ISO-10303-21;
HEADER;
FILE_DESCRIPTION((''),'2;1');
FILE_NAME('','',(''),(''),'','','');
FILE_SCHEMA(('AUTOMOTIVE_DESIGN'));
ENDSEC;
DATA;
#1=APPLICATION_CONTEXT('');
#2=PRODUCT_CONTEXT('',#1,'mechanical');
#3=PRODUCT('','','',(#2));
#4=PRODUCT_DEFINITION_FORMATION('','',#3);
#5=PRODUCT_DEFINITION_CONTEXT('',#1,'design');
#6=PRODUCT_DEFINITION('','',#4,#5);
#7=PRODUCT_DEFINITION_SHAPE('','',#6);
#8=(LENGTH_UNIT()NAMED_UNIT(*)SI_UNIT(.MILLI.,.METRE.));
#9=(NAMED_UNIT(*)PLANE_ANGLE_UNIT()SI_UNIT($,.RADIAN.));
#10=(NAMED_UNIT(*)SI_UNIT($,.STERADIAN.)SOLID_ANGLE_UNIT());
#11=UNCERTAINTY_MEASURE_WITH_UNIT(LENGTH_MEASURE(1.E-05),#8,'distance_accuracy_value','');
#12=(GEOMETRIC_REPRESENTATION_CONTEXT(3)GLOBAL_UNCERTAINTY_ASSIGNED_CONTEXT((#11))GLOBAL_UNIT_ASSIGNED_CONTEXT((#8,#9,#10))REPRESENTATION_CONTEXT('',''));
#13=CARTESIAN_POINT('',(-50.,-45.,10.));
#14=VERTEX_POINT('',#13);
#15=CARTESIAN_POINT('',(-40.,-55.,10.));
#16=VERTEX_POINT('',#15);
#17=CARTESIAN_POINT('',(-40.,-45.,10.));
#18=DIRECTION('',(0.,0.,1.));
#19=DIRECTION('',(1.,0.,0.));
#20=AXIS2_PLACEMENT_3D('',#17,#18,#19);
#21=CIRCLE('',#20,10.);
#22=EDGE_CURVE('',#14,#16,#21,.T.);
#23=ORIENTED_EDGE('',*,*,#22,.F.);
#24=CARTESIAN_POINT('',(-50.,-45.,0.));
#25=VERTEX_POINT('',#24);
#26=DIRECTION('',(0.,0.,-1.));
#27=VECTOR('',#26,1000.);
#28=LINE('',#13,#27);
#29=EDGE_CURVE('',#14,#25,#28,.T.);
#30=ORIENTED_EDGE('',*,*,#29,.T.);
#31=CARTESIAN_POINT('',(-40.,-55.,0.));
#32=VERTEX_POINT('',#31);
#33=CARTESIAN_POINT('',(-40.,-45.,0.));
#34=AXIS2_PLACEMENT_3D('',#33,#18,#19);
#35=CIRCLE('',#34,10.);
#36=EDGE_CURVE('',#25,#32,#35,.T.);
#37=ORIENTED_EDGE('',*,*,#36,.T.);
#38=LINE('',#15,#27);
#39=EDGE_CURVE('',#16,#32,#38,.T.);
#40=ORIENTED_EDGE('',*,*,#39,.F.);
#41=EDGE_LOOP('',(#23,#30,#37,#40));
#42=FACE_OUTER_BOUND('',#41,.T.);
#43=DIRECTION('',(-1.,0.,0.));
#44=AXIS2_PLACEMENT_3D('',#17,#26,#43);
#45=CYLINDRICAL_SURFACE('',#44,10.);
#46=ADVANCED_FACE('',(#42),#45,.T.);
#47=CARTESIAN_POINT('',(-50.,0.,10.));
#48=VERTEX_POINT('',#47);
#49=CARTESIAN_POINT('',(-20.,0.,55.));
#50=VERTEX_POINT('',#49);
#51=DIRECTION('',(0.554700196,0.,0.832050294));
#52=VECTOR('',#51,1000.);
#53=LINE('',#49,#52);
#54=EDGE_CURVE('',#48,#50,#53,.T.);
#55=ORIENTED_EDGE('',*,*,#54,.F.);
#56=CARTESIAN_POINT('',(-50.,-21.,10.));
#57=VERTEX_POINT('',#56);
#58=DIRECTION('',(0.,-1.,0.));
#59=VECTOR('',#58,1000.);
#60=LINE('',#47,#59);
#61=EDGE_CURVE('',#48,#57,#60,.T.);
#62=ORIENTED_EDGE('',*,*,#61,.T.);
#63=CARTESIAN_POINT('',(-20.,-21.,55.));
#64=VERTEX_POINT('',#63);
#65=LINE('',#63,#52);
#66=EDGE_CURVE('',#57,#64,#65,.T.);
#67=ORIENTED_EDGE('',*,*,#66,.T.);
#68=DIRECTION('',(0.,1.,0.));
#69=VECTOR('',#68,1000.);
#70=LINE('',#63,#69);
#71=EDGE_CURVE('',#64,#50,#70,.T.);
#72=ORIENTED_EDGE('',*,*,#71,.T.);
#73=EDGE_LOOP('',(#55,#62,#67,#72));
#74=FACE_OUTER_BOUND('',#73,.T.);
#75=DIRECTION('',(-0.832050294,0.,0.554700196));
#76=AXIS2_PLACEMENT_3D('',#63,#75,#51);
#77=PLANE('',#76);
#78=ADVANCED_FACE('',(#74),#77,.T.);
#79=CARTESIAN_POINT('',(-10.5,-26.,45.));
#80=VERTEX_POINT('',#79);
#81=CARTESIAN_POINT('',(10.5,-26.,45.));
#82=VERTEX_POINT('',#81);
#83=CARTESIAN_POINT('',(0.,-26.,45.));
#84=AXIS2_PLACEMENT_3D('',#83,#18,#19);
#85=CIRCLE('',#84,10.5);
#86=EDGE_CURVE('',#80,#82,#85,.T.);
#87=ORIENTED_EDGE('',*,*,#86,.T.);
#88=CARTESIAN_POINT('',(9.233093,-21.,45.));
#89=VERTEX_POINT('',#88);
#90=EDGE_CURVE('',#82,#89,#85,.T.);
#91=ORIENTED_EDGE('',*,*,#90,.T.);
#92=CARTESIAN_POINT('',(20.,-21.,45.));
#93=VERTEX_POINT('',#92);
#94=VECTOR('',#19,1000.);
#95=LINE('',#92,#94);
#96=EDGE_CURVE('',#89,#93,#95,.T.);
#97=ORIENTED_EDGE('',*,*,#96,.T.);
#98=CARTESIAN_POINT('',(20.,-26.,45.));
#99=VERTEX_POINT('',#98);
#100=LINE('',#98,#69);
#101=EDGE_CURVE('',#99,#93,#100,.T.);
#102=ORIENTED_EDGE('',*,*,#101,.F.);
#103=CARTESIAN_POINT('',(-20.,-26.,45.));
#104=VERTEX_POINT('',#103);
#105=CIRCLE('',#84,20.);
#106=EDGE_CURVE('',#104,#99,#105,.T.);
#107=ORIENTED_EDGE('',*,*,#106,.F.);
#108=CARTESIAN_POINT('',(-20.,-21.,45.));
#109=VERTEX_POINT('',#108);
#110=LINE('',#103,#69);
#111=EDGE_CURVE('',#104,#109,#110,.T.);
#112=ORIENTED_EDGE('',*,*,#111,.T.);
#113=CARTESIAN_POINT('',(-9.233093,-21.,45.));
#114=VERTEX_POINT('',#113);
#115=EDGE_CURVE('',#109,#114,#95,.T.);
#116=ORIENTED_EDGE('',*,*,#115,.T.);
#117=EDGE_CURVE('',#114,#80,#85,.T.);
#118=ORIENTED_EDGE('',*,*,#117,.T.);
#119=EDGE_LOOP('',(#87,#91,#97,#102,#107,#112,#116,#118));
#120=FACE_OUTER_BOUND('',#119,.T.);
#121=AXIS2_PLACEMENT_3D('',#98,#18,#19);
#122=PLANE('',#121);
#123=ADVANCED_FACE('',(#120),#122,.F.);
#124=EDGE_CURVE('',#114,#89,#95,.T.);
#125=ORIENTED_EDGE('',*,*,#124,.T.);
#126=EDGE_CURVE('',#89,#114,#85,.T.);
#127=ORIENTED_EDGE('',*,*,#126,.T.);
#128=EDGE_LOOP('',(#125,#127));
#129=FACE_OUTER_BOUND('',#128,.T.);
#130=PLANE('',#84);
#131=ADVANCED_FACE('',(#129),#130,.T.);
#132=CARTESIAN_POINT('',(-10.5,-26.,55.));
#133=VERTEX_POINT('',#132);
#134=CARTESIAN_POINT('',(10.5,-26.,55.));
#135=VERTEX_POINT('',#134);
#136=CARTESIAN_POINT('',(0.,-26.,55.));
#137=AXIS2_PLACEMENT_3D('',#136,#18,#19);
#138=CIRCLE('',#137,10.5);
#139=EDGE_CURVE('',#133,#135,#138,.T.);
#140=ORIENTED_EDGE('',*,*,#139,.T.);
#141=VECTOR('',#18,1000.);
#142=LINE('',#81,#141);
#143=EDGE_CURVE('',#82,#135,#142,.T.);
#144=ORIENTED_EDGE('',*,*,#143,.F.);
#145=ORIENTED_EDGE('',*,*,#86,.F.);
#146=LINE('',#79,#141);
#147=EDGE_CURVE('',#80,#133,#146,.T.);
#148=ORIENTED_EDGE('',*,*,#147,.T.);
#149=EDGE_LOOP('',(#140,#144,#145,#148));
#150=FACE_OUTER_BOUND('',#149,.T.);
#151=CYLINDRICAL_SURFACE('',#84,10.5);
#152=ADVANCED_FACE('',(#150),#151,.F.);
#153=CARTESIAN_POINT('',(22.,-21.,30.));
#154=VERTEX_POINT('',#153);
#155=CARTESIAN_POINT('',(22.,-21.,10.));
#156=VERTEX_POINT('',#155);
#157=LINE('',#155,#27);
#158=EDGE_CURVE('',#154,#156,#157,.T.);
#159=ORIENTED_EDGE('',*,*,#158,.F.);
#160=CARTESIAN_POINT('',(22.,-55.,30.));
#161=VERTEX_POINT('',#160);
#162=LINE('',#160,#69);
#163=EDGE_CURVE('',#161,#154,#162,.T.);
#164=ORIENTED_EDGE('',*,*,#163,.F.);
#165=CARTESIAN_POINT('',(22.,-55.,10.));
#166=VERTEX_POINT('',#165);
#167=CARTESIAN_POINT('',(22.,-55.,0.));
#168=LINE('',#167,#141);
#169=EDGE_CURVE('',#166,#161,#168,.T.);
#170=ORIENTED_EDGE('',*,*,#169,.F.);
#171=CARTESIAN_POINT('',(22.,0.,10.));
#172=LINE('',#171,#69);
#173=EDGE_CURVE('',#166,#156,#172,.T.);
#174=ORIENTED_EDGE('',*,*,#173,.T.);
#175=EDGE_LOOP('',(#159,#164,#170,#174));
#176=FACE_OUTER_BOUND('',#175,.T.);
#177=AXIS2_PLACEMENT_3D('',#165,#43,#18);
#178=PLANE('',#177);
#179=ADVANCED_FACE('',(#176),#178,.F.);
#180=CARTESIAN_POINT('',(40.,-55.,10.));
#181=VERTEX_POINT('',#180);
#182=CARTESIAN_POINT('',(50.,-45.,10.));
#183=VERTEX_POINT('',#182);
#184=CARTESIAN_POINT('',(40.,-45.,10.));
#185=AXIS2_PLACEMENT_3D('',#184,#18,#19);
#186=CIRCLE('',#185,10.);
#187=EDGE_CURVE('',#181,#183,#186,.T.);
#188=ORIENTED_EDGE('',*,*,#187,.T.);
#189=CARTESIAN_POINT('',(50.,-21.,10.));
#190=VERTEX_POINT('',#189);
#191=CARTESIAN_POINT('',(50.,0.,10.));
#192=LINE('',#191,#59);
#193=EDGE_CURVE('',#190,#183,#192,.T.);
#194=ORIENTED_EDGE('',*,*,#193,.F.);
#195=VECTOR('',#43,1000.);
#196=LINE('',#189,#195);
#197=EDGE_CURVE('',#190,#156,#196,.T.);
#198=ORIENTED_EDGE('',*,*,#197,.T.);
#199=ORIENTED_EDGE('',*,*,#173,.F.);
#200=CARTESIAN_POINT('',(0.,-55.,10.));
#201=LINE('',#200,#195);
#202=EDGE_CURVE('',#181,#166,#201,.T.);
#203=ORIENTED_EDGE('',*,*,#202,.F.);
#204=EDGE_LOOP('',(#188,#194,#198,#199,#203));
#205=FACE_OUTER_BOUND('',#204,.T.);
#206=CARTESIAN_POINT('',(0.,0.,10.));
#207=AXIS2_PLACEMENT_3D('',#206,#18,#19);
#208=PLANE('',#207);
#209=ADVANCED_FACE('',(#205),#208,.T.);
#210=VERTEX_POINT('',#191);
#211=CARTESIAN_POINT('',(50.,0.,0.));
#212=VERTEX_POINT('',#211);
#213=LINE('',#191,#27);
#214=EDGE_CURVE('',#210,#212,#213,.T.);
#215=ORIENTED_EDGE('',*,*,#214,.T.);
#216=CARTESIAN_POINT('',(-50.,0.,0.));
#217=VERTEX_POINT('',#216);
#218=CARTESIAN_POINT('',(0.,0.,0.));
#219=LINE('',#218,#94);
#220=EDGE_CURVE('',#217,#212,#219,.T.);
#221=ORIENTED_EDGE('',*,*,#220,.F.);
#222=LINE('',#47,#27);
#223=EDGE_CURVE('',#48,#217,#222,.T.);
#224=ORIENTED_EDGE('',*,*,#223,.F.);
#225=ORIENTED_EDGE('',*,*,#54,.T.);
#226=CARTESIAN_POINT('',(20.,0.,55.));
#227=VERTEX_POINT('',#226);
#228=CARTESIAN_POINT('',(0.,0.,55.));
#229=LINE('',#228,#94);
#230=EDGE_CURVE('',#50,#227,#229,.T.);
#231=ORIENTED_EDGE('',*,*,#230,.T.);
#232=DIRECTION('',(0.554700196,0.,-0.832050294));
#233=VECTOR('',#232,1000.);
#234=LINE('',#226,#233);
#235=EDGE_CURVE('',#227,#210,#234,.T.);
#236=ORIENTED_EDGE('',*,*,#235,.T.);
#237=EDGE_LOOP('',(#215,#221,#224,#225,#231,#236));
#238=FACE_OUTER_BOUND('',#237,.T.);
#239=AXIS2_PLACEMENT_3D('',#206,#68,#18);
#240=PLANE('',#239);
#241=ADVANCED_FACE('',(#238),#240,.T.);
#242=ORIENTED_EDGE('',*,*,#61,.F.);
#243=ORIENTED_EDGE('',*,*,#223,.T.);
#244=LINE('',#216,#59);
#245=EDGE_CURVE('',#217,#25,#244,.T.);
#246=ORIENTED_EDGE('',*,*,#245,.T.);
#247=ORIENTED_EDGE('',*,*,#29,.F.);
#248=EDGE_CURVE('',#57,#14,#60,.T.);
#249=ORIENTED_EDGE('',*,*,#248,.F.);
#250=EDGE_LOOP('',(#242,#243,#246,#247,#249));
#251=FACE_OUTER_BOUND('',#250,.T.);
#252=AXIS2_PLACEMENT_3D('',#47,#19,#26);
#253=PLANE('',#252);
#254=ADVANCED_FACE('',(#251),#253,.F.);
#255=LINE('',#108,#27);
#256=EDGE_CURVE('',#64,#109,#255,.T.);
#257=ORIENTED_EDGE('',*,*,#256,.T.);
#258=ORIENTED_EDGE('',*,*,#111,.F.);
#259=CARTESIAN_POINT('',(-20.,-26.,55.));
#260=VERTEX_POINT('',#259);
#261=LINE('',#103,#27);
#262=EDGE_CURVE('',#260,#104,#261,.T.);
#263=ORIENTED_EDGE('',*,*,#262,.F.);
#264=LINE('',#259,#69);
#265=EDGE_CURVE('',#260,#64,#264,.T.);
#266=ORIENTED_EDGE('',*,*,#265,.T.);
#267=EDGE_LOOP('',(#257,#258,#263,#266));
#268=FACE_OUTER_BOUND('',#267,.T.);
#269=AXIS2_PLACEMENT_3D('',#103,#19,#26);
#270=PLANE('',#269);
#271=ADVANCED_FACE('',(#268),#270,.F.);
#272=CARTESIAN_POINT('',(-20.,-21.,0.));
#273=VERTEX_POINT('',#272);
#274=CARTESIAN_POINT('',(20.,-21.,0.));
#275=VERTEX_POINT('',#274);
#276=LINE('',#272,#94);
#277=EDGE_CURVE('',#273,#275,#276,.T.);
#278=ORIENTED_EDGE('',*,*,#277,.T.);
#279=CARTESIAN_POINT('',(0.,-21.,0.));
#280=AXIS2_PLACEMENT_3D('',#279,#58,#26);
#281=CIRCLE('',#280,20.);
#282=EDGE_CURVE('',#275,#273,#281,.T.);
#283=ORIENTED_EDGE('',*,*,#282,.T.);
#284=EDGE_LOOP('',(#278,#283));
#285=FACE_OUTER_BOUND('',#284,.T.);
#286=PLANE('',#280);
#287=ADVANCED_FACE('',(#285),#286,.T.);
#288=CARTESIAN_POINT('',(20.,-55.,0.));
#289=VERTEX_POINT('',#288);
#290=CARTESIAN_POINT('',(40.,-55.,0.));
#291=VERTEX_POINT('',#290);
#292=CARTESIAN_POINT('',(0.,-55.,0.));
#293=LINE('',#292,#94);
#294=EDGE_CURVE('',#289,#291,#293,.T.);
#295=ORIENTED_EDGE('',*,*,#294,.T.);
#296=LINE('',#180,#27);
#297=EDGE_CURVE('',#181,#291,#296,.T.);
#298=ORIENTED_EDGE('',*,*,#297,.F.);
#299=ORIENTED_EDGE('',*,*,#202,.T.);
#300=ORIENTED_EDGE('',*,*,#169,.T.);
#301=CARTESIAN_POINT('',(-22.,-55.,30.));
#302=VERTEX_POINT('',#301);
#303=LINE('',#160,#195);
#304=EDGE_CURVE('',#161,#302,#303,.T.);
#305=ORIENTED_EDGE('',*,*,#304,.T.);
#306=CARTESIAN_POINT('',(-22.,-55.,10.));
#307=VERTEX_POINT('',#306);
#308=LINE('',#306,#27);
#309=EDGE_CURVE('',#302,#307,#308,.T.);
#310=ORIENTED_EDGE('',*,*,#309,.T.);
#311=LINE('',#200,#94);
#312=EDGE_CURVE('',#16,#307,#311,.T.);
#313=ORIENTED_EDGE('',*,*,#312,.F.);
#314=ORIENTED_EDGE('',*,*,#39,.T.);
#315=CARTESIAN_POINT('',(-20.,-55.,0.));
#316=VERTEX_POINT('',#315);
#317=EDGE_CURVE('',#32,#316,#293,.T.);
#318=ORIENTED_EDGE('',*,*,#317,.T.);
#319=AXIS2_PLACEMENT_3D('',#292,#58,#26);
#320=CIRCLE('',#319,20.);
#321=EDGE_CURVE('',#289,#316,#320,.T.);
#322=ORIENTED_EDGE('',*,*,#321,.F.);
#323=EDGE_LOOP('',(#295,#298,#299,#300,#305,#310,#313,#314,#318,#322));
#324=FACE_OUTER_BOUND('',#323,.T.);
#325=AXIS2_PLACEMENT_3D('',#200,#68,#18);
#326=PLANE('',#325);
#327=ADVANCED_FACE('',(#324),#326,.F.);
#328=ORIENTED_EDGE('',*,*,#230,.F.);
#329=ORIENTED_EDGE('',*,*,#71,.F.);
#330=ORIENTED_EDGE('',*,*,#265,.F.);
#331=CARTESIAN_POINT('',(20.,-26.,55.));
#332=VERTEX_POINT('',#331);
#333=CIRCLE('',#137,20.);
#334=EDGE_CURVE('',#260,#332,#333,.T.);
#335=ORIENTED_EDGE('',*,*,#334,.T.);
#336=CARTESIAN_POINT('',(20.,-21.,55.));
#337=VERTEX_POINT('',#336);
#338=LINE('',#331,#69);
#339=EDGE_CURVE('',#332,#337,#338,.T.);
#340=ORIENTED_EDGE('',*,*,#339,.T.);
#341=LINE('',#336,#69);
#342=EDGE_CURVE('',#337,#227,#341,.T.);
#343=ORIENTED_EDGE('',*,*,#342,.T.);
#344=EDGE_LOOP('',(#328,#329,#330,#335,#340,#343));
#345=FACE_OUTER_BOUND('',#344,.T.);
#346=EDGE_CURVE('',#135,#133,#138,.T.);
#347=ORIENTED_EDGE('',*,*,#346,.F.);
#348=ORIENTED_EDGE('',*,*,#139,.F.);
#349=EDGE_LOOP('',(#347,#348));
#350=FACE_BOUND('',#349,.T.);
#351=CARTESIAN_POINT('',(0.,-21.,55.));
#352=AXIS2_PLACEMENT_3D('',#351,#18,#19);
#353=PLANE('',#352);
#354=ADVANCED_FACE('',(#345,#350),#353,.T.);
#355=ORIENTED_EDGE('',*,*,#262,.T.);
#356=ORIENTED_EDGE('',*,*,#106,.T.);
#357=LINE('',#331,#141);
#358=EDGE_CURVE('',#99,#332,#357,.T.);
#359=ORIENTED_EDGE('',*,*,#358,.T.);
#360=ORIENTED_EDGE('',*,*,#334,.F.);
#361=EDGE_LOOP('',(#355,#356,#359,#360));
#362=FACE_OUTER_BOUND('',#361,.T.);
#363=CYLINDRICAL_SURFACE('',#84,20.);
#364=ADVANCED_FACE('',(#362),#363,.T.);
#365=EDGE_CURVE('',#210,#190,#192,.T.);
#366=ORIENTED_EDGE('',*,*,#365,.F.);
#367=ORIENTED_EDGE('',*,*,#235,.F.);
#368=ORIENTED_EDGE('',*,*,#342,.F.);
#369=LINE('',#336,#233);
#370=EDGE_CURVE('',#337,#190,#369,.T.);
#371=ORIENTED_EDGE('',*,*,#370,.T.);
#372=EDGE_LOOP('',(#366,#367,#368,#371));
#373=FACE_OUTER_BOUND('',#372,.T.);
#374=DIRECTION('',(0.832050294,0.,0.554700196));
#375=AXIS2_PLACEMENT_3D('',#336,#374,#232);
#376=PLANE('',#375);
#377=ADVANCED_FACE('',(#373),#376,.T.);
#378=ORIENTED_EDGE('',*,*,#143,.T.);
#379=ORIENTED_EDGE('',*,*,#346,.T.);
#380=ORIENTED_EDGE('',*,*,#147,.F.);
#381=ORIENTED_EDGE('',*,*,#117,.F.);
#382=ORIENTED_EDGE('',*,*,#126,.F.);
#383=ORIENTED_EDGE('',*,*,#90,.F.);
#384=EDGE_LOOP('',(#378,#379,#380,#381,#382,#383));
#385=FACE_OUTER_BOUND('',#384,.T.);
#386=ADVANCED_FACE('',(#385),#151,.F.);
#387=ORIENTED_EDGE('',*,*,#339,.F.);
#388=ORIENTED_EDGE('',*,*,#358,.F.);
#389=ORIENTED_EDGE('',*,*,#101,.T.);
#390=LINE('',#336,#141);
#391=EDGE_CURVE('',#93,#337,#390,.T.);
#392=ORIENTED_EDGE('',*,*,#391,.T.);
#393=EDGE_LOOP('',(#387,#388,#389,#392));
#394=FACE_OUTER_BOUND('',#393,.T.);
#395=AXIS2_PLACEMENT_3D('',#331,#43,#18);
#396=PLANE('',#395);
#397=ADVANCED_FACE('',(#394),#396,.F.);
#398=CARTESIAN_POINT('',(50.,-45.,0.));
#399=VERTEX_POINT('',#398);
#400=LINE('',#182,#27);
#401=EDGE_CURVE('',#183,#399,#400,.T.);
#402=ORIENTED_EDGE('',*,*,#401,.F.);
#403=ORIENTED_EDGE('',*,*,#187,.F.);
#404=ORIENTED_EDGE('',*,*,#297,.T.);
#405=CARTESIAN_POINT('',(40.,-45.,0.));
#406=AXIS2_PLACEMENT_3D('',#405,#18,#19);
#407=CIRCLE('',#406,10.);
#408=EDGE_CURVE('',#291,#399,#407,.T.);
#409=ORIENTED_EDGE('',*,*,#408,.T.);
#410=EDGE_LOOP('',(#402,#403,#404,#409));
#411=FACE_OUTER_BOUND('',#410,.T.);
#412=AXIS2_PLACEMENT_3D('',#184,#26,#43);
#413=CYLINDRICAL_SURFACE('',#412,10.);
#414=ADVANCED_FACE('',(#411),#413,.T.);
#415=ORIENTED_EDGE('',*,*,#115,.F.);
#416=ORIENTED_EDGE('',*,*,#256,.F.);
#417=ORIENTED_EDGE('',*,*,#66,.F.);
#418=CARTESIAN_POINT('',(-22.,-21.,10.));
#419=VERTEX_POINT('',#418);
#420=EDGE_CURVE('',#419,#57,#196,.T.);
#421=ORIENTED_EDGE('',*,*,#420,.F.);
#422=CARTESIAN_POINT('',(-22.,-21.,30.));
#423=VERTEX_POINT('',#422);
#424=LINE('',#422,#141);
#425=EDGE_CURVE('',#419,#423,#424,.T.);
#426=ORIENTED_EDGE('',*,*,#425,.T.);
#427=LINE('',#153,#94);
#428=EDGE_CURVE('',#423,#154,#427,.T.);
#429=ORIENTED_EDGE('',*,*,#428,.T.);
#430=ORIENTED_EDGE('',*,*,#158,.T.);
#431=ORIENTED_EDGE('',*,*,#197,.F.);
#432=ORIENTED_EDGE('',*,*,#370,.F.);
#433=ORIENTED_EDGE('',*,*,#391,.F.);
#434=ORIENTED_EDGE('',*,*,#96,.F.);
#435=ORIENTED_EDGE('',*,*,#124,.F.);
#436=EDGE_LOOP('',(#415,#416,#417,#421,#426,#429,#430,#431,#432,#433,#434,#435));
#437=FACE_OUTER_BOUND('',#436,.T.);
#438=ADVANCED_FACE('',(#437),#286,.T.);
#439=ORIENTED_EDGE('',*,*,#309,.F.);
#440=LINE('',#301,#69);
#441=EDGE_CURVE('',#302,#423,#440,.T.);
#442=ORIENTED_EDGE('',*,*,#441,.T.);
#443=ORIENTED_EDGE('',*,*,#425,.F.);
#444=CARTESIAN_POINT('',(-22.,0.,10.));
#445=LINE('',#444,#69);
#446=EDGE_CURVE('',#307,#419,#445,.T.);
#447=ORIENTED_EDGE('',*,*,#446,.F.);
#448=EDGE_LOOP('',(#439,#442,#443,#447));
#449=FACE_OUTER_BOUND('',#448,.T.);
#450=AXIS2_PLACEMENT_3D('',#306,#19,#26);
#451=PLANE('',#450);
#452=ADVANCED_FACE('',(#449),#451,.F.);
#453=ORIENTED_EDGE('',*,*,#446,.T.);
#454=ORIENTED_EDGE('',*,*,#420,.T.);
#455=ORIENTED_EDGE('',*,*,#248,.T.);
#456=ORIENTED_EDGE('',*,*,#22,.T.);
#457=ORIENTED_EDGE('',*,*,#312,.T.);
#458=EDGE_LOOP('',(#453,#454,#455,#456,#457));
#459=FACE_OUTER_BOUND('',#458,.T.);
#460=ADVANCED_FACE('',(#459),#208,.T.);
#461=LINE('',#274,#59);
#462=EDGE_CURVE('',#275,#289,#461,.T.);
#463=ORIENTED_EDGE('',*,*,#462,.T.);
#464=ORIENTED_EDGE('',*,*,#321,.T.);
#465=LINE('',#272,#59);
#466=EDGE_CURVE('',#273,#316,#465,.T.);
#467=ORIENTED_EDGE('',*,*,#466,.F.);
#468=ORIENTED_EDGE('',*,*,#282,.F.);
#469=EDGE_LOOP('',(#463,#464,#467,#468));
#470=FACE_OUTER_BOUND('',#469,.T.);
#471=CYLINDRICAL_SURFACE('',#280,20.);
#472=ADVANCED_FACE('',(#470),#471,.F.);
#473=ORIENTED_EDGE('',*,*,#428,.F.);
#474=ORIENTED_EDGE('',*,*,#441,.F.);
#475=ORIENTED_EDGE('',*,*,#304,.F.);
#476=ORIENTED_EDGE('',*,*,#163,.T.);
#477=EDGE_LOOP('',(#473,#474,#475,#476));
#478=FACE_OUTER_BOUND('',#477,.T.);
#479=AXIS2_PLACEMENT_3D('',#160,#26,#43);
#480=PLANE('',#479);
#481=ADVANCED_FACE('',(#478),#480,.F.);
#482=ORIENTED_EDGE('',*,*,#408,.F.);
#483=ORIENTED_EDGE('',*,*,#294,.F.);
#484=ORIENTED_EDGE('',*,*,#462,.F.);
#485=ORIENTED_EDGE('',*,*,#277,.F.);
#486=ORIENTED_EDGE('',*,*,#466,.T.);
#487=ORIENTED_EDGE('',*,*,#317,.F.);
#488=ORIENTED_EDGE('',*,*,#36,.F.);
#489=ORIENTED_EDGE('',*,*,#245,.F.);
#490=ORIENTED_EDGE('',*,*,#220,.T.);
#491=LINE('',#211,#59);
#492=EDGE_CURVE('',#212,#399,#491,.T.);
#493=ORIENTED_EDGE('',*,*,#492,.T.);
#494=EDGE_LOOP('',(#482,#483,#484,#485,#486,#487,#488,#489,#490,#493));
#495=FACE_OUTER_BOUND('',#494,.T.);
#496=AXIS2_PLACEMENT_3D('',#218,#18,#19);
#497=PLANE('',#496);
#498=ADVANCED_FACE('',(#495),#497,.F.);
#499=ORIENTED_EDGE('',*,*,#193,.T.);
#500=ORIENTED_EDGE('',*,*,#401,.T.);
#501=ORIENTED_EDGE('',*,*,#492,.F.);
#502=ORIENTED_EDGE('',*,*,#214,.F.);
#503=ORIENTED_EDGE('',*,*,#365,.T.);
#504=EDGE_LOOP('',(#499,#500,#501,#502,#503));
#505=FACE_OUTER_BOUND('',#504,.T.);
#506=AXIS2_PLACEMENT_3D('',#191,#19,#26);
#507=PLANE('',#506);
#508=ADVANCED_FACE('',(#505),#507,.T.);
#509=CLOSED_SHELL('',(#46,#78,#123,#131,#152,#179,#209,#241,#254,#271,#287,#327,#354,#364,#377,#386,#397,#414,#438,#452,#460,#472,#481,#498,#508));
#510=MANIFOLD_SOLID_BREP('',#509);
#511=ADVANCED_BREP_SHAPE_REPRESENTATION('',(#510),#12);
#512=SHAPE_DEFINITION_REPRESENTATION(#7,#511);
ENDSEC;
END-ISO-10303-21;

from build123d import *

# Parameters (mm, degrees)
BASE_PROFILE_10MM_DEPTH = 10
UPPER_BLOCK_30MM_DEPTH  = 30
PAD_SKETCH_W            = 44
PAD_SKETCH_H            = 20
PAD_4MM_DEPTH           = 4
PROFILE_CUT_34MM_DEPTH  = 34
SIDE_WALL_21MM_DEPTH    = 21
RAIL_SKETCH_W           = 40
RAIL_SKETCH_H           = 10
RAIL_5MM_DEPTH          = 5
LUG_BOSS_10MM_DEPTH     = 10
LUG_HOLE_SKETCH_21_R    = 10.5
LUG_HOLE_21_DEPTH       = 10


with BuildPart() as part:
    # Base Profile Sketch → Base Profile 10mm (new body)
    with BuildSketch(Plane.XY):
        with BuildLine():
            Line((40, -55), (22, -55))
            Line((22, -55), (22, -25))
            Line((22, -25), (-22, -25))
            Line((-22, -25), (-22, -55))
            Line((-22, -55), (-40, -55))
            ThreePointArc((-40, -55), (-47.071067812, -52.071067812), (-50, -45))
            Line((-50, -45), (-50, 0))
            Line((-50, 0), (0, 0))
            Line((0, 0), (50, 0))
            Line((50, 0), (50, -45))
            ThreePointArc((50, -45), (47.071067812, -52.071067812), (40, -55))
        make_face()
    extrude(amount=BASE_PROFILE_10MM_DEPTH)

    # Upper Block Sketch → Upper Block 30mm (add)
    with BuildSketch(Plane.XZ.offset(25)):
        Polygon((-22, 10), (-22, 30), (22, 30), (22, 10), (22, 0), (-22, 0), align=None)
    extrude(amount=UPPER_BLOCK_30MM_DEPTH)

    # Pad Sketch → Pad 4mm (add)
    with BuildSketch(Plane(origin=(0, -25, 0), x_dir=(1, 0, 0), z_dir=(0, 1, 0))):
        with Locations((0, -20)):
            Rectangle(PAD_SKETCH_W, PAD_SKETCH_H)
    extrude(amount=PAD_4MM_DEPTH)

    # Profile Cut Sketch → Profile Cut 34mm (cut)
    with BuildSketch(Plane.XZ.offset(55)):
        with BuildLine():
            Line((-20, 0), (20, 0))
            ThreePointArc((20, 0), (0, 20), (-20, 0))
        make_face()
    extrude(amount=-PROFILE_CUT_34MM_DEPTH, mode=Mode.SUBTRACT)

    # Side Wall Sketch → Side Wall 21mm (add)
    with BuildSketch(Plane(origin=(0, 0, 0), x_dir=(1, 0, 0), z_dir=(0, 1, 0))):
        Polygon((0, -55), (20, -55), (50, -10), (-50, -10), (-20, -55), align=None)
    extrude(amount=-SIDE_WALL_21MM_DEPTH)

    # Rail Sketch → Rail 5mm (add)
    with BuildSketch(Plane.XZ.offset(21)):
        with Locations((0, 50)):
            Rectangle(RAIL_SKETCH_W, RAIL_SKETCH_H)
    extrude(amount=RAIL_5MM_DEPTH)

    # Lug Sketch → Lug Boss 10mm (add)
    with BuildSketch(Plane.XY.offset(55)):
        with BuildLine():
            Line((-20, -26), (20, -26))
            ThreePointArc((20, -26), (0, -46), (-20, -26))
        make_face()
    extrude(amount=-LUG_BOSS_10MM_DEPTH)

    # Lug Hole Sketch Ø21 → Lug Hole Ø21 (cut)
    with BuildSketch(Plane.XY.offset(55)):
        with Locations((0, -26)):
            Circle(LUG_HOLE_SKETCH_21_R)
    extrude(amount=-LUG_HOLE_21_DEPTH, mode=Mode.SUBTRACT)


solid = part.part
